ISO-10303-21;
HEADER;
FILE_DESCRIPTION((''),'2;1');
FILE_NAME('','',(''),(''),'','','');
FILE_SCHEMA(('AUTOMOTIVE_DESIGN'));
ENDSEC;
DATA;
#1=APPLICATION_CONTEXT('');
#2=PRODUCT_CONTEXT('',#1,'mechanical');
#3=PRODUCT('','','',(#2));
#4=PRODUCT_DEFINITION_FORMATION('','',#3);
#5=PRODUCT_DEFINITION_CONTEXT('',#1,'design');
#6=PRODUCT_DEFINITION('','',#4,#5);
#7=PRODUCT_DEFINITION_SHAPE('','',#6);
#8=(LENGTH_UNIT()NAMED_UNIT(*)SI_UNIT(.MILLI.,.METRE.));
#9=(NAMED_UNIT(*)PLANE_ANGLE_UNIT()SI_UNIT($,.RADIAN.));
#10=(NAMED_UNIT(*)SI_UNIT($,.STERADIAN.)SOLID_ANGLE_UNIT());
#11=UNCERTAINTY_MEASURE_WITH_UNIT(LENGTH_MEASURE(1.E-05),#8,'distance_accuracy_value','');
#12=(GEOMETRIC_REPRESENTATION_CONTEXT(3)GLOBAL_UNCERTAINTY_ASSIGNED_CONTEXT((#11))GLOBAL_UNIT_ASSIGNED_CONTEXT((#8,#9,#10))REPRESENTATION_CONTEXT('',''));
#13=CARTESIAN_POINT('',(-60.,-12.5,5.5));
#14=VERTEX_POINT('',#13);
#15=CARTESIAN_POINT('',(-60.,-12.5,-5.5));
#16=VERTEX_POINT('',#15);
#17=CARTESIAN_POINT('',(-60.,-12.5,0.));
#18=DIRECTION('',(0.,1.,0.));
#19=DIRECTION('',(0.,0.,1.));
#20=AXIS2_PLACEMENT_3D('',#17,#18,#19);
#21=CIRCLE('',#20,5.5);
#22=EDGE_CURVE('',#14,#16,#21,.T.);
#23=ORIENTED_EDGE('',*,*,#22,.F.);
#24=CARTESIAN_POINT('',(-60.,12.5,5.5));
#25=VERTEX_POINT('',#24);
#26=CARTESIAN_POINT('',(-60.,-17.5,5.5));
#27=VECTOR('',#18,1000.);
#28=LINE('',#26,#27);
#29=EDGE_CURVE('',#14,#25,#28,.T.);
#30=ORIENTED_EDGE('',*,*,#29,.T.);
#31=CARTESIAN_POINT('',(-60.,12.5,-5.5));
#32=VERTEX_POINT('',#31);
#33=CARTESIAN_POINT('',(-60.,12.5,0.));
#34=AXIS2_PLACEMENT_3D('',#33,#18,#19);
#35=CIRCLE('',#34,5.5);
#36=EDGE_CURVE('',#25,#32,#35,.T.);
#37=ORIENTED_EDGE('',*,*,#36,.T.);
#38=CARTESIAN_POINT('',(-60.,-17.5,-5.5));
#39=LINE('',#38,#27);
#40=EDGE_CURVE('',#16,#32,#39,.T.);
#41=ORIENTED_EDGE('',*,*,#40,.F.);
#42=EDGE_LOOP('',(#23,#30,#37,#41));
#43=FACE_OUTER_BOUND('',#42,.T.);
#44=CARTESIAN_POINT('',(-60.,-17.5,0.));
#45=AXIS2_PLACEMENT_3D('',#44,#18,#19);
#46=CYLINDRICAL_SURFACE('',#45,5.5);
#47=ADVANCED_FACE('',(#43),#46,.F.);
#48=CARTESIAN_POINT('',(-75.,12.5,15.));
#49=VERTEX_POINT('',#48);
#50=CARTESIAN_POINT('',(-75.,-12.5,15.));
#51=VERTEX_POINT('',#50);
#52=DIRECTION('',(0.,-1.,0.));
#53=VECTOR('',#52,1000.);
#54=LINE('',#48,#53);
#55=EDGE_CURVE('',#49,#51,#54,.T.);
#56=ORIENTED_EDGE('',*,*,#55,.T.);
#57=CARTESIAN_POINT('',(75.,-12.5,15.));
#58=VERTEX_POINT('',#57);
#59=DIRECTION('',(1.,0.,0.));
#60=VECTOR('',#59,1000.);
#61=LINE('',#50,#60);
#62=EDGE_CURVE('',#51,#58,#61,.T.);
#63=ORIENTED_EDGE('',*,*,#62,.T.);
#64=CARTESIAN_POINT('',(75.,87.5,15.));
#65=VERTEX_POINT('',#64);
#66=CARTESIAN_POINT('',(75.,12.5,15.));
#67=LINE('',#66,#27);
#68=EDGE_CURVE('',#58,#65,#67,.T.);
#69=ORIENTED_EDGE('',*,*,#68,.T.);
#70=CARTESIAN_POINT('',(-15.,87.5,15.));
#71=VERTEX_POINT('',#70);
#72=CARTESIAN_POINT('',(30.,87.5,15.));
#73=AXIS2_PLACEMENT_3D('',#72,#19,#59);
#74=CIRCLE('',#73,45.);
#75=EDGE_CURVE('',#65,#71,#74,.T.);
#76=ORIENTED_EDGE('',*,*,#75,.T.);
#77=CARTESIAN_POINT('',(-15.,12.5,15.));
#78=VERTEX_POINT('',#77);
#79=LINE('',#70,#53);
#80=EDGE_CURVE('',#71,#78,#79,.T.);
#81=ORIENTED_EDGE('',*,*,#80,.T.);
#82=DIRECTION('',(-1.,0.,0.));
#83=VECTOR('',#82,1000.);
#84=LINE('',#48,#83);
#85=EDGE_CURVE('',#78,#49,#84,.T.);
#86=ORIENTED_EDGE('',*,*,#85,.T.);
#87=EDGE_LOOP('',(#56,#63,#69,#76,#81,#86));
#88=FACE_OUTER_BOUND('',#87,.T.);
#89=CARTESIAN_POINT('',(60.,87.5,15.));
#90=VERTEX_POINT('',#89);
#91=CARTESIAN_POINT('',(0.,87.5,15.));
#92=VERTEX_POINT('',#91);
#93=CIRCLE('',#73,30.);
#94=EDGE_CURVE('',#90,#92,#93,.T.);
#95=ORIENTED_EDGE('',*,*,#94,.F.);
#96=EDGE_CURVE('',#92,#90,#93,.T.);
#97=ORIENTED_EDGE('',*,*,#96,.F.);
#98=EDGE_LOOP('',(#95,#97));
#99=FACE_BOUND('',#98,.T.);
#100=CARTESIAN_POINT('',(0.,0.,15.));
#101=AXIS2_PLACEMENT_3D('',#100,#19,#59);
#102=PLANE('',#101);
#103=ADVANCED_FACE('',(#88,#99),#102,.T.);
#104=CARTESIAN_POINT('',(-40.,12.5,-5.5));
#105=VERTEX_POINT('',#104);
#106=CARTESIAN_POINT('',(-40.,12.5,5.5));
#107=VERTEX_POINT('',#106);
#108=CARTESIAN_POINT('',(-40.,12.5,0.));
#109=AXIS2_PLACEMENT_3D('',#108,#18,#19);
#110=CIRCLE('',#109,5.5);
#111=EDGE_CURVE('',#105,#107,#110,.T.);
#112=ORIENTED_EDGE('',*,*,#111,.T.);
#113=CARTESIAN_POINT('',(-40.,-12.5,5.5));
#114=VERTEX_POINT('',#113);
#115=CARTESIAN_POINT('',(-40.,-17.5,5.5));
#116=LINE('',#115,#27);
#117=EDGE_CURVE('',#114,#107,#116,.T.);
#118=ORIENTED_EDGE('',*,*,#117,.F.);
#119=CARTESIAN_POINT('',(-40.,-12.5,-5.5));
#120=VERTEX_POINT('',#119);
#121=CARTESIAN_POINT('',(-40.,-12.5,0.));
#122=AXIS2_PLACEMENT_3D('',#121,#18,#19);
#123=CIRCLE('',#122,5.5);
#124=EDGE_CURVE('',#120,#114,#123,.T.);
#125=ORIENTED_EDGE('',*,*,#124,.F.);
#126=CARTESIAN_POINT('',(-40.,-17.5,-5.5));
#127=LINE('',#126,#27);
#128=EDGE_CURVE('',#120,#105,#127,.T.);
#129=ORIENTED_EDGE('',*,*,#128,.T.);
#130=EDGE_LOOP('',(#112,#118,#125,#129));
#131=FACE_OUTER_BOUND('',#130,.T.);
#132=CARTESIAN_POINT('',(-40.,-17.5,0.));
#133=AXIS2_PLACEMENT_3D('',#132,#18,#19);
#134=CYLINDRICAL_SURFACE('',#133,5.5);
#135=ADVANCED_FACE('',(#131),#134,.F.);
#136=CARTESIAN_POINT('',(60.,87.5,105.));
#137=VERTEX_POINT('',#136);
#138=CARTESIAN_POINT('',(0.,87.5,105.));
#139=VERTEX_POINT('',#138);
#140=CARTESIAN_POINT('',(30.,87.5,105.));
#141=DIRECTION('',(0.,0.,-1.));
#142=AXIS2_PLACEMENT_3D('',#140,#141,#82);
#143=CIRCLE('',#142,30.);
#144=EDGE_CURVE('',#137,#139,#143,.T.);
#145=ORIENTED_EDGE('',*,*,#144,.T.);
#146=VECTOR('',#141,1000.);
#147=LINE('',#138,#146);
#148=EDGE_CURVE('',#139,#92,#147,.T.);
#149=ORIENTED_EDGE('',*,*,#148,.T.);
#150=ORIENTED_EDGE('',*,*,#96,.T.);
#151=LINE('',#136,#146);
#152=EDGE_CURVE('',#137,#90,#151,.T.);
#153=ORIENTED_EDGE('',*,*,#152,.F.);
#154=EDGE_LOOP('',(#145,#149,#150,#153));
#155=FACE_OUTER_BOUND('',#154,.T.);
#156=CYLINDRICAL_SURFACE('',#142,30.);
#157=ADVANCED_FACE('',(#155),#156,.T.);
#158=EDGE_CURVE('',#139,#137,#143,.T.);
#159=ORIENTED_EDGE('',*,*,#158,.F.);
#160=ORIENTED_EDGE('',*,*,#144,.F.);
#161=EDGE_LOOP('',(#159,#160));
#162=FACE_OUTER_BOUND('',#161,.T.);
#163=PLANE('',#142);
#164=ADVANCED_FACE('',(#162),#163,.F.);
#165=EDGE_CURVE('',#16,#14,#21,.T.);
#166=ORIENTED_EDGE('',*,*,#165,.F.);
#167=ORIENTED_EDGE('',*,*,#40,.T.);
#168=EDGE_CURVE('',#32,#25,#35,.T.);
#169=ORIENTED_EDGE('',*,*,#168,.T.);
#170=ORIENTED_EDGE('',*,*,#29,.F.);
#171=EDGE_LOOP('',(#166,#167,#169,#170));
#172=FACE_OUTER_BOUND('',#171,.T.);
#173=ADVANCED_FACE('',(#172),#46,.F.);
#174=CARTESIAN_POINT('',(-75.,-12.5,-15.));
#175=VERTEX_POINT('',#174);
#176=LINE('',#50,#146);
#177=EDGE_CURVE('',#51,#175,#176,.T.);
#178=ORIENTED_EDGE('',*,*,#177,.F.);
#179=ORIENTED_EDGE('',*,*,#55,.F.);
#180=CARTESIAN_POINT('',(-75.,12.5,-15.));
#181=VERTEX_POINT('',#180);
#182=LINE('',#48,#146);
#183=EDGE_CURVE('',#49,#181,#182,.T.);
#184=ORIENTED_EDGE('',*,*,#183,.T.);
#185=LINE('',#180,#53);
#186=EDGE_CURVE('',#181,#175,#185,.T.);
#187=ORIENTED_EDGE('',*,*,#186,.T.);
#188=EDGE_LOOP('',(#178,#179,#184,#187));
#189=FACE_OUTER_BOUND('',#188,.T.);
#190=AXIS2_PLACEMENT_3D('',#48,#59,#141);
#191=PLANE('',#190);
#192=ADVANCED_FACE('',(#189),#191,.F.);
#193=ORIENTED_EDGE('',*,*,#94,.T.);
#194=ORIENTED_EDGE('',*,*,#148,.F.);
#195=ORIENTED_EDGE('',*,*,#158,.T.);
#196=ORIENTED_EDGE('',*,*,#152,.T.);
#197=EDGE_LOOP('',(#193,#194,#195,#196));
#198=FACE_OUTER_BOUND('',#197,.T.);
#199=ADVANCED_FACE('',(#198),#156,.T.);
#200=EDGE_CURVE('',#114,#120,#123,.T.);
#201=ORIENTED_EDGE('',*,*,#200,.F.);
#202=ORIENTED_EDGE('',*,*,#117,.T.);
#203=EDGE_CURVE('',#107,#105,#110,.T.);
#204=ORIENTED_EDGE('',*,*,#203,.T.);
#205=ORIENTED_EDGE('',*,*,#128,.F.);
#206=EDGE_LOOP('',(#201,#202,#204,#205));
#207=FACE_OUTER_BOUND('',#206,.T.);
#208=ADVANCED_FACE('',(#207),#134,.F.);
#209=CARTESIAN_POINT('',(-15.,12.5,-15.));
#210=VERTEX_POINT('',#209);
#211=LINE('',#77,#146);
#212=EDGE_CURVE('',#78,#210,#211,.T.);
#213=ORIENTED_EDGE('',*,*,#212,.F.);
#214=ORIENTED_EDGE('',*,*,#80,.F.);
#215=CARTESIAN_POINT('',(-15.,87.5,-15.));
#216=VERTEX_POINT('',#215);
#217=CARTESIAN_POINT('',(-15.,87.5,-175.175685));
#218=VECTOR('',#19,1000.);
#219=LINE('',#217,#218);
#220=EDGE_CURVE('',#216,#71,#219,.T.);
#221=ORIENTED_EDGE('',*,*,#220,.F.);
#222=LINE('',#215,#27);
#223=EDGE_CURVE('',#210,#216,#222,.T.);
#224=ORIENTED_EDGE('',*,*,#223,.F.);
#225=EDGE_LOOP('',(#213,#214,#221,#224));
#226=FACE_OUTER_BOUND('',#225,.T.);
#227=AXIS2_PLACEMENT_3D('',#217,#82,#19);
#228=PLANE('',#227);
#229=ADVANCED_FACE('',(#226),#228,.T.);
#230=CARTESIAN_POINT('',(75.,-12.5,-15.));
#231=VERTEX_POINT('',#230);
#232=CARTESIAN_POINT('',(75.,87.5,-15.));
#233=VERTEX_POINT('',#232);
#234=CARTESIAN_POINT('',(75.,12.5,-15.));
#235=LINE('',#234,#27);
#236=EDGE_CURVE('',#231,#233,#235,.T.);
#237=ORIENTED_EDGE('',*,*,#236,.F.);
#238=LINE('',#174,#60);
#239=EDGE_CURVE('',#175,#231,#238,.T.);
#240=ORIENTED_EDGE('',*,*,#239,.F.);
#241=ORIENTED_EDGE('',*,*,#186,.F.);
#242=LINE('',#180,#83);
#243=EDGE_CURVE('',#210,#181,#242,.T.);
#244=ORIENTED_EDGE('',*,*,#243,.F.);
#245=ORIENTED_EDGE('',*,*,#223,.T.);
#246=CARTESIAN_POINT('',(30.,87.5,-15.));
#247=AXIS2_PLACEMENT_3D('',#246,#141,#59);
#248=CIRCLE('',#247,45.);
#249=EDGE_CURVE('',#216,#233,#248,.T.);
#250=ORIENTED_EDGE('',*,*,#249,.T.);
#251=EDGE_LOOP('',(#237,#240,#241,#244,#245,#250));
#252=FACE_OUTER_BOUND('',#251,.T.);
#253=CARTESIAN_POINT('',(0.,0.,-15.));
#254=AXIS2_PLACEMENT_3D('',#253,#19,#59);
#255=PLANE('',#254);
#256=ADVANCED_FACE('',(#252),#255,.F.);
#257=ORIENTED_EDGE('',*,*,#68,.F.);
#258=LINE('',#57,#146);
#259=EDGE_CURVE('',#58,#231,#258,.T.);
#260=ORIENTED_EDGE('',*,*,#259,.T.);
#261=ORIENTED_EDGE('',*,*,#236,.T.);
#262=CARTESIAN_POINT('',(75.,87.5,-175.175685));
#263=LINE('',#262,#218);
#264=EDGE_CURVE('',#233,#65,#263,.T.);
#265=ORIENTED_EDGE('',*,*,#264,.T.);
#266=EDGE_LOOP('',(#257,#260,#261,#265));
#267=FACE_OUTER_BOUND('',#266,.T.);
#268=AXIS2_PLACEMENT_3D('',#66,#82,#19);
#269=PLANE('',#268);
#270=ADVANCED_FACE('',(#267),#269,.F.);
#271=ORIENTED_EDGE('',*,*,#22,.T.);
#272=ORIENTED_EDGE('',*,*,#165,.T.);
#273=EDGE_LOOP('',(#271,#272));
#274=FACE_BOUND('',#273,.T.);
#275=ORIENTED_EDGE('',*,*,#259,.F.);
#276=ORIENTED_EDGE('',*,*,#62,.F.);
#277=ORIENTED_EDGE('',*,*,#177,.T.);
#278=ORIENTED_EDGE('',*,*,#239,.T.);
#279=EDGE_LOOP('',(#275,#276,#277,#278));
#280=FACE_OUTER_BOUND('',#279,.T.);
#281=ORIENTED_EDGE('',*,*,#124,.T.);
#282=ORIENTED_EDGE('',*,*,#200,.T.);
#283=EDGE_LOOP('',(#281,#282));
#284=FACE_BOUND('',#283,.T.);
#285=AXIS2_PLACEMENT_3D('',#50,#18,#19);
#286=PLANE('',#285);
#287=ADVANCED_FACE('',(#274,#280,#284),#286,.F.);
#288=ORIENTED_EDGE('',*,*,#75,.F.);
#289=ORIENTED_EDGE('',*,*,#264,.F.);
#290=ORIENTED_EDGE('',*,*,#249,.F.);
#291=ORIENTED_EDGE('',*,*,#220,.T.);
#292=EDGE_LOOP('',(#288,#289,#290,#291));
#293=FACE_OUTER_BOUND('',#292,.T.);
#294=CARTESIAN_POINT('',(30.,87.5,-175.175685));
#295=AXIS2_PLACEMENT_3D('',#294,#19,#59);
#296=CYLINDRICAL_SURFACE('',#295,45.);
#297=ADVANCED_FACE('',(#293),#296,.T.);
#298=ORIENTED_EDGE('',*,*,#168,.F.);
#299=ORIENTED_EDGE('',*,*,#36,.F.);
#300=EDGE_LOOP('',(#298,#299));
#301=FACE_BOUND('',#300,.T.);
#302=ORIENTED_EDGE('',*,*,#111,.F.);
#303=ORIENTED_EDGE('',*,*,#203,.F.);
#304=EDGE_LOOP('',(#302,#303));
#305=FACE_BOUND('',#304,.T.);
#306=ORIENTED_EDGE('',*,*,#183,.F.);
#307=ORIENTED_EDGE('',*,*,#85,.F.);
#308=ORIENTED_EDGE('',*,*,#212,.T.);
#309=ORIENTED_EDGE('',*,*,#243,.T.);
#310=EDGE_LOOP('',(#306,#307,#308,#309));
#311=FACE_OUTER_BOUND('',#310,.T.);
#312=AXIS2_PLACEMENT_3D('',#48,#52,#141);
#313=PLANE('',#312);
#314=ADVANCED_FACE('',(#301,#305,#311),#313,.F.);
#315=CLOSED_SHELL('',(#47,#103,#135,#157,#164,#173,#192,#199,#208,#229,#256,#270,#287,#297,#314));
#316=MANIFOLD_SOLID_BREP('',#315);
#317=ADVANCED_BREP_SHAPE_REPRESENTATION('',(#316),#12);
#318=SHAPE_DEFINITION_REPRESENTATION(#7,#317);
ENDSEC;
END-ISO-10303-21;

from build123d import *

# Parameters (mm, degrees)
SKETCH2_W           = 150
SKETCH2_H           = 25
BOSS_EXTRUDE1_DEPTH = 15
SKETCH3_R           = 30
BOSS_EXTRUDE2_DEPTH = 30
SKETCH4_R           = 5.5
CUT_EXTRUDE1_DEPTH  = 30
BOSS_EXTRUDE3_START = -120
SKETCH5_R           = 30
BOSS_EXTRUDE3_DEPTH = 120


with BuildPart() as part:
    # Sketch2 → Boss-Extrude1 (new, symmetric)
    with BuildSketch(Plane.XY):
        Rectangle(SKETCH2_W, SKETCH2_H)
    extrude(amount=BOSS_EXTRUDE1_DEPTH, both=True)

    # Sketch3 → Boss-Extrude2 (add)
    with BuildSketch(Plane.XY.offset(15)):
        with BuildLine():
            Line((-15, 87.5), (-15, 0))
            Line((-15, 0), (75, 0))
            Line((75, 0), (75, 87.5))
            ThreePointArc((75, 87.5), (30, 132.5), (-15, 87.5))
        make_face()
        with Locations((30, 87.5)):
            Circle(SKETCH3_R, mode=Mode.SUBTRACT)
    extrude(amount=-BOSS_EXTRUDE2_DEPTH)

    # Sketch4 → Cut-Extrude1 (cut)
    with BuildSketch(Plane(origin=(0, 12.5, 0), x_dir=(1, 0, 0), z_dir=(0, 1, 0))):
        with Locations(Location((-60, 0, 0), (0, 0, 270))):
            Circle(SKETCH4_R)
        with Locations(Location((-40, 0, 0), (0, 0, 270))):
            Circle(SKETCH4_R)
    extrude(amount=-CUT_EXTRUDE1_DEPTH, mode=Mode.SUBTRACT)

    # Sketch5 → Boss-Extrude3 (add)
    with BuildSketch(Plane(origin=(0, 0, -15), x_dir=(-1, 0, 0), z_dir=(0, 0, -1)).offset(BOSS_EXTRUDE3_START)):
        with Locations((-30, 87.5)):
            Circle(SKETCH5_R)
    extrude(amount=BOSS_EXTRUDE3_DEPTH)


solid = part.part
